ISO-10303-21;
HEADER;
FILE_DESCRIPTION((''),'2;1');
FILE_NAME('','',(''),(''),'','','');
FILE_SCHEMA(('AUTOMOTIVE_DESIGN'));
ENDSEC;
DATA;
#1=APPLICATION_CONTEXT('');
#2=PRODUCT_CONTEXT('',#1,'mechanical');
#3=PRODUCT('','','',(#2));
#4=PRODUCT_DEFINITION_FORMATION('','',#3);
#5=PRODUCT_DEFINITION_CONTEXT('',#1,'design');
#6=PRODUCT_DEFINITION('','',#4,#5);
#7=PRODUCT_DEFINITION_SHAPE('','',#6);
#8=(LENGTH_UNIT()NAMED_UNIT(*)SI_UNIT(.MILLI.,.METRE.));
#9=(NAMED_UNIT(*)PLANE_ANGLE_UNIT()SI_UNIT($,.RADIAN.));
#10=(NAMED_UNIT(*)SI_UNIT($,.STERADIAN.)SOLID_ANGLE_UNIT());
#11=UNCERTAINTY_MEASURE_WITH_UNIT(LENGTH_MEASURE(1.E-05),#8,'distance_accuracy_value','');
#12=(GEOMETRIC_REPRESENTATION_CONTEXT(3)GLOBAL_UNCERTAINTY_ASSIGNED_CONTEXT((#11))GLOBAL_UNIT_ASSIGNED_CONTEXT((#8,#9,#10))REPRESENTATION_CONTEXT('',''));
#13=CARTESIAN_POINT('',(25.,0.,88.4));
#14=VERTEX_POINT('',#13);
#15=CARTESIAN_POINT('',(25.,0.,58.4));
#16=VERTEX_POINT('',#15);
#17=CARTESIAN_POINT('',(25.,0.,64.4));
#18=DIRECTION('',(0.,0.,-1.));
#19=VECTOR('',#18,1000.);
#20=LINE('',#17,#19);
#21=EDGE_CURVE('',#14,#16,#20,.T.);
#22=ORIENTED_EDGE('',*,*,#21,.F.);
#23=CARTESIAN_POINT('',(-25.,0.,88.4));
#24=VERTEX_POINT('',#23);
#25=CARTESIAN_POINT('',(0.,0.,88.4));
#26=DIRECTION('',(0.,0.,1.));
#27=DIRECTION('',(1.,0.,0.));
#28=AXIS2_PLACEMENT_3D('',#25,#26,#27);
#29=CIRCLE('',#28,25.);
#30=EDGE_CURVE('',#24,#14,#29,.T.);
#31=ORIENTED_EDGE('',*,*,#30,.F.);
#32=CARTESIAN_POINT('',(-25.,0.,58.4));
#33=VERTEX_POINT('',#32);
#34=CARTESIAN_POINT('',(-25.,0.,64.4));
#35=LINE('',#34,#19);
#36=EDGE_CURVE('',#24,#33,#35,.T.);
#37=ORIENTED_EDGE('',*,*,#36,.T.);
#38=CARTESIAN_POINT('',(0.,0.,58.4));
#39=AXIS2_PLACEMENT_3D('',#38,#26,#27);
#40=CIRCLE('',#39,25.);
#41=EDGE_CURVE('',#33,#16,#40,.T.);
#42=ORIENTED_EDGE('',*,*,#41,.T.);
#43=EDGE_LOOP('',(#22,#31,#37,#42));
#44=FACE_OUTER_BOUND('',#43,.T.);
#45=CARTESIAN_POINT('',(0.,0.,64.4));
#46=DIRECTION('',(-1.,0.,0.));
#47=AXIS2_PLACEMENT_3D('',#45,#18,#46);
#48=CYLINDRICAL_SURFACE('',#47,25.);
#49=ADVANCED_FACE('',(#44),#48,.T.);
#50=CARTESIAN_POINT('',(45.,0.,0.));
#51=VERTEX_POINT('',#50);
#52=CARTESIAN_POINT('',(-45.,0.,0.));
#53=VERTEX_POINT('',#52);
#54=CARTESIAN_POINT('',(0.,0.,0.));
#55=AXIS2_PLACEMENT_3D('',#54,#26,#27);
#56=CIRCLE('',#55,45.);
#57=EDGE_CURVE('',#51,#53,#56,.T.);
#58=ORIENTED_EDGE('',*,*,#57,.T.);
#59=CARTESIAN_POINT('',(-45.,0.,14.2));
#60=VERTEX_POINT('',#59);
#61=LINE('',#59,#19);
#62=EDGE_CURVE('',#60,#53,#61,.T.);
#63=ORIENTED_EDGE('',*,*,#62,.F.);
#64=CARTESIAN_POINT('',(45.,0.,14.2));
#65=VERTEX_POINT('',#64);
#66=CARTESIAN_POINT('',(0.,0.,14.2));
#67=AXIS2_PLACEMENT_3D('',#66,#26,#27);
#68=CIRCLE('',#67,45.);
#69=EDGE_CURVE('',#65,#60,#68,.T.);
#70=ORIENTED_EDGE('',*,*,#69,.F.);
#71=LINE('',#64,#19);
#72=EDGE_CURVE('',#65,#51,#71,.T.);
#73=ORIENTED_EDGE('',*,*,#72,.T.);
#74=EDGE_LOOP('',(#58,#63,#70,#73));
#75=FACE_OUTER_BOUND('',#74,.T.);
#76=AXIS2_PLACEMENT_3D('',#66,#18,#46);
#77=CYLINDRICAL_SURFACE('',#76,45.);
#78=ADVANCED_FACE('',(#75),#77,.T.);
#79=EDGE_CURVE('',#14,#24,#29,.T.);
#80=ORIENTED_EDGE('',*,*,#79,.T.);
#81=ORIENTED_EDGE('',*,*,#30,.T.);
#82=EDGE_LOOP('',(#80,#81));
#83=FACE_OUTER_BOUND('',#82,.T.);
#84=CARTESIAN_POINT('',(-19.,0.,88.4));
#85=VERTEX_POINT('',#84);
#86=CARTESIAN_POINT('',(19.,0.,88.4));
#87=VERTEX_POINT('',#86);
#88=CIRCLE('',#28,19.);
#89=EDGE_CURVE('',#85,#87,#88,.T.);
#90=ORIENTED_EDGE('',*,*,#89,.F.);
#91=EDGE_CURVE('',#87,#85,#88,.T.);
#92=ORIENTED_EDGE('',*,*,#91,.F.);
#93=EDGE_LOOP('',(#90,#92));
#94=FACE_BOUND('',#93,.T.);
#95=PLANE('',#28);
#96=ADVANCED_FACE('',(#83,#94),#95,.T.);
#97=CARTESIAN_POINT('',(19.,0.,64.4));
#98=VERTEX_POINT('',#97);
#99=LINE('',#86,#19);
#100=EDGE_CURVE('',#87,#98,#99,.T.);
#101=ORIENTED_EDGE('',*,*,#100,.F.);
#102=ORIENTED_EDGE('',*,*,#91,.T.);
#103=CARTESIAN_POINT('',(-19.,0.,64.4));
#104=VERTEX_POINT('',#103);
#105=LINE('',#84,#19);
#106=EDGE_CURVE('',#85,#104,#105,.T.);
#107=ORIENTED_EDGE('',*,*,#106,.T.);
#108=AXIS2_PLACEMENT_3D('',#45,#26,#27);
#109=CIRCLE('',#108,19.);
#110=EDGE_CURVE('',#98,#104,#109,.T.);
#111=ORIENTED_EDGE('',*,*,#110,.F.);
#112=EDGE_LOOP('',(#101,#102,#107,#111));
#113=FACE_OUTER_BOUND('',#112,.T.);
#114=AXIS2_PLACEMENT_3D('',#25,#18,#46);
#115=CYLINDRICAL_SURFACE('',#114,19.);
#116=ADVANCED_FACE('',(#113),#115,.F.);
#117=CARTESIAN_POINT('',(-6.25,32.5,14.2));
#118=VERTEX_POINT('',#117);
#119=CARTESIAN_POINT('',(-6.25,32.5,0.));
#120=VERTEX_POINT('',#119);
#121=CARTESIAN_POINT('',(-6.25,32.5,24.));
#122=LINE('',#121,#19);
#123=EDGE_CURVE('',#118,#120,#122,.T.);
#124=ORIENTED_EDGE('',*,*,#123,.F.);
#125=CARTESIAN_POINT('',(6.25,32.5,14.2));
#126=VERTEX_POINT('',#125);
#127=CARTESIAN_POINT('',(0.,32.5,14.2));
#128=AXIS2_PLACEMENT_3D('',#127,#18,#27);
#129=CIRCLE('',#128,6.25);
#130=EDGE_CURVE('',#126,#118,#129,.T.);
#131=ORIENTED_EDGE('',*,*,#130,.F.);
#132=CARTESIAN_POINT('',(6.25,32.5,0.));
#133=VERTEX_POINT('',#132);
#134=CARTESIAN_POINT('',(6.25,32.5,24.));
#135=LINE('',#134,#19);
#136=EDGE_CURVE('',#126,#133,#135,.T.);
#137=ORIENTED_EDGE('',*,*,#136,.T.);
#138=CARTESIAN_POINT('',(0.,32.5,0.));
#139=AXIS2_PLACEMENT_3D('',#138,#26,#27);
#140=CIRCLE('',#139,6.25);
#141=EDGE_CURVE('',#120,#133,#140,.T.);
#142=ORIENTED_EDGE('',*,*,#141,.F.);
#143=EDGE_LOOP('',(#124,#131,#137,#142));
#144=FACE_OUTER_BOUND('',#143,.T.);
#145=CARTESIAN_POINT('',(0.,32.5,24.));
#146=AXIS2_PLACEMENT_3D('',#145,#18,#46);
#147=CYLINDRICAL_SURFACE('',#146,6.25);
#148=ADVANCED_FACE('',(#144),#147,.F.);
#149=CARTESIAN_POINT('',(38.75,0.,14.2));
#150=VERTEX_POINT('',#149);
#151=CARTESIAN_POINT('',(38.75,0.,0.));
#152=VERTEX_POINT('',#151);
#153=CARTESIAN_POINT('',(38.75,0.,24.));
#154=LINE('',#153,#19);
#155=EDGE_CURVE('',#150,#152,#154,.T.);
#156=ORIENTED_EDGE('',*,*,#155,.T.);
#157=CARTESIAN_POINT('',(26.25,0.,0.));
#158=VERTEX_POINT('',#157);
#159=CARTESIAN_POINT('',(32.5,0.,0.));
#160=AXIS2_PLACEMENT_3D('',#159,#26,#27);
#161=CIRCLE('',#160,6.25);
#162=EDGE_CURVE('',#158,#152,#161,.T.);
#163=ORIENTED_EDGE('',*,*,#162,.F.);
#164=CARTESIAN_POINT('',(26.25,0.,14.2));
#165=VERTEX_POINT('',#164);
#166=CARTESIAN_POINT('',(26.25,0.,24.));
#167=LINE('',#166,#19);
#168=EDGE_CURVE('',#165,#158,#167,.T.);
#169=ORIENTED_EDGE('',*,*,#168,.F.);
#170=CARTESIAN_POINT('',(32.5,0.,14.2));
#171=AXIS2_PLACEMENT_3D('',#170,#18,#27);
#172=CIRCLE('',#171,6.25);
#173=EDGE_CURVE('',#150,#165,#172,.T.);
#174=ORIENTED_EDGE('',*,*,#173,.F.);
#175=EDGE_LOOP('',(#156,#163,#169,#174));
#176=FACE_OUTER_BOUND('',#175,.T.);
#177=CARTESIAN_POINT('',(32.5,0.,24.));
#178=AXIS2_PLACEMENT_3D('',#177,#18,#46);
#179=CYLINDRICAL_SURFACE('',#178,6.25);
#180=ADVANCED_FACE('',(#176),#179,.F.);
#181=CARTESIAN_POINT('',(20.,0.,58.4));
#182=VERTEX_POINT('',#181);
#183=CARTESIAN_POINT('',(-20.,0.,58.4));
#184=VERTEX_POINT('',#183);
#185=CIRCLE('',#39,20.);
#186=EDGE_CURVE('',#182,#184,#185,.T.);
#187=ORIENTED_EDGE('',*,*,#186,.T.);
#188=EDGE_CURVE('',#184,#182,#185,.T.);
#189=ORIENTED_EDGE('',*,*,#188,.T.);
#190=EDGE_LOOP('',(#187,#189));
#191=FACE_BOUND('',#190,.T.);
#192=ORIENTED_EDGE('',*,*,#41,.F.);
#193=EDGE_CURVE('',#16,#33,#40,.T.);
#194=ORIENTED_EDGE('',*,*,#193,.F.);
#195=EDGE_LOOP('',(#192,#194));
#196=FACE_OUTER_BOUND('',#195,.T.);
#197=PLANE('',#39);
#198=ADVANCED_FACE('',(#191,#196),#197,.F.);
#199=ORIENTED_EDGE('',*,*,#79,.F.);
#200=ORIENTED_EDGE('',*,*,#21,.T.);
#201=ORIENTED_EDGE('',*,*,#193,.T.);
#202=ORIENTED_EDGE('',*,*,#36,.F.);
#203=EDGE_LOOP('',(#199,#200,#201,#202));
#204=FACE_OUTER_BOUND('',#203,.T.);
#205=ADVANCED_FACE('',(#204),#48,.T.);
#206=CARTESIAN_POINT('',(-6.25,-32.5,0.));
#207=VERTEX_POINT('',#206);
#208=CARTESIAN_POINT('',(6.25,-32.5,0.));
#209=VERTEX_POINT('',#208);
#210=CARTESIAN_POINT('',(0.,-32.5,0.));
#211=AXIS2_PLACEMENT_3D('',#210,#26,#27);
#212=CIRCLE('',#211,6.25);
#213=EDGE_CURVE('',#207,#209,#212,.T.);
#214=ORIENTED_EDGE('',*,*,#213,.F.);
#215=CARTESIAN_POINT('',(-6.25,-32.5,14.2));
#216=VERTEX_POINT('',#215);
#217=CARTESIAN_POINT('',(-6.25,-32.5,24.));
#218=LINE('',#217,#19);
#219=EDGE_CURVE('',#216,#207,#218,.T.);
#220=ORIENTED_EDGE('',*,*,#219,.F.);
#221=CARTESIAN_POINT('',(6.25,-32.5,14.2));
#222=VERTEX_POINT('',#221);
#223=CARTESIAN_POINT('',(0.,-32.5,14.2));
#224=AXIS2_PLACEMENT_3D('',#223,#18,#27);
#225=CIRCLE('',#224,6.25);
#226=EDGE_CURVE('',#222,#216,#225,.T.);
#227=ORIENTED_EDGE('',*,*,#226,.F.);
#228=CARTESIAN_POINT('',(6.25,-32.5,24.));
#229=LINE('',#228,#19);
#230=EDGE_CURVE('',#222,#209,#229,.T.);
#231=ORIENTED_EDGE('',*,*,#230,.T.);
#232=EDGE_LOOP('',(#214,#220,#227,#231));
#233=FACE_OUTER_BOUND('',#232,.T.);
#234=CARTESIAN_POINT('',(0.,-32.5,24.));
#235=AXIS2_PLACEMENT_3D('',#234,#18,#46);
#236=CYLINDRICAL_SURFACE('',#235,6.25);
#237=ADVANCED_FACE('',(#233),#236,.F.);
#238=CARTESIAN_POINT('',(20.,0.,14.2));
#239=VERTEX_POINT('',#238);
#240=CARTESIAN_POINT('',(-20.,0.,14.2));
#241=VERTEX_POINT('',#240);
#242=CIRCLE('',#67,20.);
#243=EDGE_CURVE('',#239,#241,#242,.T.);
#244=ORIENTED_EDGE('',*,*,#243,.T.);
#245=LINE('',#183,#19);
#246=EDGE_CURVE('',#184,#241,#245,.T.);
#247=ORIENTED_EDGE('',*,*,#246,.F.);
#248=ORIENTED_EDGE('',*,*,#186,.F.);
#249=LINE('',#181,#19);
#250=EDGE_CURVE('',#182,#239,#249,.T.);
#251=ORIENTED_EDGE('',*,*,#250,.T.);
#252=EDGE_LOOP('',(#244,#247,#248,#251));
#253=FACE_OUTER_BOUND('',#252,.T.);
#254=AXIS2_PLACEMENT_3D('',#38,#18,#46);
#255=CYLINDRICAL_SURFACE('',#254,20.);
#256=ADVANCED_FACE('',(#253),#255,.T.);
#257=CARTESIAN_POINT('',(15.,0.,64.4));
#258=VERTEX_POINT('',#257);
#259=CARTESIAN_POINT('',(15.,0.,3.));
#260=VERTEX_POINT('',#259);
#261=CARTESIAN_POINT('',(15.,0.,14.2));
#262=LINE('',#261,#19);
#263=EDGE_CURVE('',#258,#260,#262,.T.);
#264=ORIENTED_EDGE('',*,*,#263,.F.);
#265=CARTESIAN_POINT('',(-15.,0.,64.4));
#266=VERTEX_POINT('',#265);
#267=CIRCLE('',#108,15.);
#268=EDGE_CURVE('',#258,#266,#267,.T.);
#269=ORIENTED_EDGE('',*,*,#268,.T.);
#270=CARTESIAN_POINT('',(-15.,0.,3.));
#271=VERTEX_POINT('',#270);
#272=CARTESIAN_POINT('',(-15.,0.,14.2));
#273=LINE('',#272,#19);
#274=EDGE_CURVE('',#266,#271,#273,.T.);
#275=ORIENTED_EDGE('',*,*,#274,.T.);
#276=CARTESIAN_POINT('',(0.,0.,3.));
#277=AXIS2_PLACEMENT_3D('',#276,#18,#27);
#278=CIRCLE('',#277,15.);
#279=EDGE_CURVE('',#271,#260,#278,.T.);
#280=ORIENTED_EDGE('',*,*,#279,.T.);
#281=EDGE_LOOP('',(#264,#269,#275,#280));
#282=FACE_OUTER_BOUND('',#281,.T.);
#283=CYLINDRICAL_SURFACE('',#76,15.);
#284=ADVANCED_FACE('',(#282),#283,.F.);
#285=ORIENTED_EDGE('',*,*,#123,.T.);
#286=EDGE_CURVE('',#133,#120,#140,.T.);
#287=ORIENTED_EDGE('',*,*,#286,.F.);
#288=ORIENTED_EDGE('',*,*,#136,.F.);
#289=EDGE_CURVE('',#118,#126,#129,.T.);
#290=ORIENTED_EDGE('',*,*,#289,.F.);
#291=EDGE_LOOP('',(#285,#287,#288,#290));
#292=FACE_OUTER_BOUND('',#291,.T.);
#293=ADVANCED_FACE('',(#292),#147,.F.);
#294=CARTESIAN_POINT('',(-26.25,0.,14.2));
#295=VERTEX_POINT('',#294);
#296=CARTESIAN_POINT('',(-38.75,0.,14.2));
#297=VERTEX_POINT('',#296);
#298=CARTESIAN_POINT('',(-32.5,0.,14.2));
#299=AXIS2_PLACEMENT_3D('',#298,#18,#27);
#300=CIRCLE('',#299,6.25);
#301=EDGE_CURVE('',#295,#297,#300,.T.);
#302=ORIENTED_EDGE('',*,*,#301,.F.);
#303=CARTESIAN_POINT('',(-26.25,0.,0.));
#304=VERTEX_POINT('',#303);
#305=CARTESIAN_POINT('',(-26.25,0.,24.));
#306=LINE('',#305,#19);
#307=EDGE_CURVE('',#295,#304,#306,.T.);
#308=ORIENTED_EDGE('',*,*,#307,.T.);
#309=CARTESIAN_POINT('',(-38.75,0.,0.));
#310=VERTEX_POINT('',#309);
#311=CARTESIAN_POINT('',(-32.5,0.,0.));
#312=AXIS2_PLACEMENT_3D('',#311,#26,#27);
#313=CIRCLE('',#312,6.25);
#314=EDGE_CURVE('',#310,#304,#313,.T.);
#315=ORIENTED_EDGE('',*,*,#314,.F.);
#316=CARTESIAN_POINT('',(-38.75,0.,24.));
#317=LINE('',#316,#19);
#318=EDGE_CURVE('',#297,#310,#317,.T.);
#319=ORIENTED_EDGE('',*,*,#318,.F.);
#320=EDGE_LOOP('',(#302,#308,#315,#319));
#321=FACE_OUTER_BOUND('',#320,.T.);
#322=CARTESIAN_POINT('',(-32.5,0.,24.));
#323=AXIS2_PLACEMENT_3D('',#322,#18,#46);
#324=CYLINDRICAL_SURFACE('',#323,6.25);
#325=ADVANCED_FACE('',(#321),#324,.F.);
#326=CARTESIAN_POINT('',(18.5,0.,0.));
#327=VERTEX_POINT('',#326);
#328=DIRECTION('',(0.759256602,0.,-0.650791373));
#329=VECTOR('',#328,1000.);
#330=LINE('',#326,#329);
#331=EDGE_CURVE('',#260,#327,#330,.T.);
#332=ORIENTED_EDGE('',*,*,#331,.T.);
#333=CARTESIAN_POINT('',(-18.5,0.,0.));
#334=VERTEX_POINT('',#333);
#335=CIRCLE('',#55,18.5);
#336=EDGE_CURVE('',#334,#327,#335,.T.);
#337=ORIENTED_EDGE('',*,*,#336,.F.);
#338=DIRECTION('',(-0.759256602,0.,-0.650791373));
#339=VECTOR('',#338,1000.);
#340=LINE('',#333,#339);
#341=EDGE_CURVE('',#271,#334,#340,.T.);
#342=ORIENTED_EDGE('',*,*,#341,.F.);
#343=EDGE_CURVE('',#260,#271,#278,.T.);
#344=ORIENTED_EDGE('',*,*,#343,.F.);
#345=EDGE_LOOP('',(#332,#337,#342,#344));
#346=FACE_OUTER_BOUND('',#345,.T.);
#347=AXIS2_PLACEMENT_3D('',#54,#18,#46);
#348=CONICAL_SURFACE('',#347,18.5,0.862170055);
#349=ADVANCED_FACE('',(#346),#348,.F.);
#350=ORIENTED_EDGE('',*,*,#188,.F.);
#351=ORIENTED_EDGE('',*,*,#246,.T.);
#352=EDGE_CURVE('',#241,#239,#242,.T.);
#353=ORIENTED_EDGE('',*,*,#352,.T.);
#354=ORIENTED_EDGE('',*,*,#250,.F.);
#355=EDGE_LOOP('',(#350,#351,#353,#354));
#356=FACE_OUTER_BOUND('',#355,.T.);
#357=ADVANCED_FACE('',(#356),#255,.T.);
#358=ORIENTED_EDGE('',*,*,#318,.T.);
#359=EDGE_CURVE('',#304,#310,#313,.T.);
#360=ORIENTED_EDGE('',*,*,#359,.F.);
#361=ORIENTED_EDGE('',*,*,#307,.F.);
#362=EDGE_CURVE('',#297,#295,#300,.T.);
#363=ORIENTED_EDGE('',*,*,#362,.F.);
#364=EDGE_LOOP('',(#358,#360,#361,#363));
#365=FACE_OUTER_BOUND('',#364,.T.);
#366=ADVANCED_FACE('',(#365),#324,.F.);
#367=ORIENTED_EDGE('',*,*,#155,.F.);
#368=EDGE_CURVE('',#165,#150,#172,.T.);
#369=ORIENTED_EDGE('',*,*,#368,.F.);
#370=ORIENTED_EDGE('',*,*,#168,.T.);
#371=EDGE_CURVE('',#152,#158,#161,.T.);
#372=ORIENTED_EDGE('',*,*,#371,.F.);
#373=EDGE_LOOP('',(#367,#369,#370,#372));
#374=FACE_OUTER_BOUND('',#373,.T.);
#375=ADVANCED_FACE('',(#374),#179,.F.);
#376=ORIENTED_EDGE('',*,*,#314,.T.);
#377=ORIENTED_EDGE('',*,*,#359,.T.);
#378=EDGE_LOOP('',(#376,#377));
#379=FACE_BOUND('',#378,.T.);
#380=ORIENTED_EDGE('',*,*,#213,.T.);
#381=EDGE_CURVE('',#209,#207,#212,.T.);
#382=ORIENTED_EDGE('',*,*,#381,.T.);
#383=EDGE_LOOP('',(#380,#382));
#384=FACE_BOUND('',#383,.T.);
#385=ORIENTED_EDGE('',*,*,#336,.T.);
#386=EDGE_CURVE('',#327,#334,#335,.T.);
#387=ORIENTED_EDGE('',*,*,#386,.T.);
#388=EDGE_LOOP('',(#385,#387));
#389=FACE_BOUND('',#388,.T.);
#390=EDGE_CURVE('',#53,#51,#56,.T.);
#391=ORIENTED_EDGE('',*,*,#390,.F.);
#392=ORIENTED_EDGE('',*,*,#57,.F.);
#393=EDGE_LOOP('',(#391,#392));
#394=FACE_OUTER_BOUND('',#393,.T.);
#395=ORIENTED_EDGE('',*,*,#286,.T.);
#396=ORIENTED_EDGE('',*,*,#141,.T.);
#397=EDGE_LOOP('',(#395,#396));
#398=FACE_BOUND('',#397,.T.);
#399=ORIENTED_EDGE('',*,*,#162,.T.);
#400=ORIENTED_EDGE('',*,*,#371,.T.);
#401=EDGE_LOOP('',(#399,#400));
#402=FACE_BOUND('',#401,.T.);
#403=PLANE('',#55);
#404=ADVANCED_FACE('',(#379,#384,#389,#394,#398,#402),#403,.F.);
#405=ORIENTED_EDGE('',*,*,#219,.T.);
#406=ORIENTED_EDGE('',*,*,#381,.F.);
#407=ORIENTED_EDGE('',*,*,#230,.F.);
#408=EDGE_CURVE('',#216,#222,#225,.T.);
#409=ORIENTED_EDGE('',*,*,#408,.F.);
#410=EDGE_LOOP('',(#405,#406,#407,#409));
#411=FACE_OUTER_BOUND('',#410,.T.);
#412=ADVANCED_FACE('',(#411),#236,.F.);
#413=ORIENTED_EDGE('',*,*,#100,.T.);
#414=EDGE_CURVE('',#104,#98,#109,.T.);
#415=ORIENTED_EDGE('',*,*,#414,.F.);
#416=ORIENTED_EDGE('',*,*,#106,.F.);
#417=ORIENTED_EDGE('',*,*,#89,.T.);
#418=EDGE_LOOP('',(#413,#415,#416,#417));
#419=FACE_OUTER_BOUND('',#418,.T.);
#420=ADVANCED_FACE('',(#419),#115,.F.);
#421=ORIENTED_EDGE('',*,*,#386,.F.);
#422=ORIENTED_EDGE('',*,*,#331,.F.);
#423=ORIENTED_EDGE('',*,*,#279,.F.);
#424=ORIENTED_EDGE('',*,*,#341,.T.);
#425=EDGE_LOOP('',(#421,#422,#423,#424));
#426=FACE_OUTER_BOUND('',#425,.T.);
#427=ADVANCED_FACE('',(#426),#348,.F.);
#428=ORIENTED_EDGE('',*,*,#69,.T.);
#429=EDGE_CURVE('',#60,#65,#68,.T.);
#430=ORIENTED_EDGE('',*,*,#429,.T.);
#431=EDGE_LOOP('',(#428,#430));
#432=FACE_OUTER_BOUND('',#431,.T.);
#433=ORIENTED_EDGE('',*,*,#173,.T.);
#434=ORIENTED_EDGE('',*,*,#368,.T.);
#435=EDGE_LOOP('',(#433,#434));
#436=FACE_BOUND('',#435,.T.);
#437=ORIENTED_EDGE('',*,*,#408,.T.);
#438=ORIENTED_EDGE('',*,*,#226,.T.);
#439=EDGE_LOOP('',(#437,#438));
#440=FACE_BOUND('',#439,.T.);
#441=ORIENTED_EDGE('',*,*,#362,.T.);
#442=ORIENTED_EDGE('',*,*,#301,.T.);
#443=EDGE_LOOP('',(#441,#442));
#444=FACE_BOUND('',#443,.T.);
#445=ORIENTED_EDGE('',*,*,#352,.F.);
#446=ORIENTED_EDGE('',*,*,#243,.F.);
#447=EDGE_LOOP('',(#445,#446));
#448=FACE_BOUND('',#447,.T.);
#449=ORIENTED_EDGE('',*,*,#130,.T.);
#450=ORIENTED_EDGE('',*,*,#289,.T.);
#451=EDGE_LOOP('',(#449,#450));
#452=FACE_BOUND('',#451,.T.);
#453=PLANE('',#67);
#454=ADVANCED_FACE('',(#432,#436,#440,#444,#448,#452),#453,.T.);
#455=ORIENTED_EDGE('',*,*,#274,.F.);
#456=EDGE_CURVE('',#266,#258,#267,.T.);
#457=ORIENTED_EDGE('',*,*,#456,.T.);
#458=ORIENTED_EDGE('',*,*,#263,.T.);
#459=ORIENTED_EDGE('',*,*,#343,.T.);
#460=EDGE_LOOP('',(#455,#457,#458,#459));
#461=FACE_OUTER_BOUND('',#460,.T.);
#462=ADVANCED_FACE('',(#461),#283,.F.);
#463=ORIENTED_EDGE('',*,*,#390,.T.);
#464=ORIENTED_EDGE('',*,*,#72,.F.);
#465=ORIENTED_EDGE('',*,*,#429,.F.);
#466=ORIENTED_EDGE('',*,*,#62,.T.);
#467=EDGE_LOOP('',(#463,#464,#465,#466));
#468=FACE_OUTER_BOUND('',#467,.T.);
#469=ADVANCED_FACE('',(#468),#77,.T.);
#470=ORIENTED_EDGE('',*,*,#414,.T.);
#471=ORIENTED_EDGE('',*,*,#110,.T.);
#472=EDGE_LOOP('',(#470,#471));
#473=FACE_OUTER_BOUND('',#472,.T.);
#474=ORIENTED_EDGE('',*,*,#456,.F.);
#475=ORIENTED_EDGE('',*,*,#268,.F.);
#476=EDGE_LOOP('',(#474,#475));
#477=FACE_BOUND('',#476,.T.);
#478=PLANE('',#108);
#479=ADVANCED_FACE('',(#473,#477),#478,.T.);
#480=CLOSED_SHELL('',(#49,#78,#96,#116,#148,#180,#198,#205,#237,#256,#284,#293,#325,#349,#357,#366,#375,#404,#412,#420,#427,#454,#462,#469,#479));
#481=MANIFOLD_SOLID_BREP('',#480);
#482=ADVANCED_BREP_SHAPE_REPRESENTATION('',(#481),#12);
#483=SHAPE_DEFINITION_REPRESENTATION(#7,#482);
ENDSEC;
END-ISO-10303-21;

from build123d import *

# Parameters (mm, degrees)
FLANGE_SKETCH_R             = 45
FLANGE_SKETCH_R_2           = 15
FLANGE_90_DEPTH             = 14.2
HUB_SKETCH_R                = 20
HUB_SKETCH_R_2              = 15
HUB_40_DEPTH                = 44.2
COLLAR_SKETCH_R             = 25
COLLAR_SKETCH_R_2           = 15
COLLAR_50_DEPTH             = 6
END_SLEEVE_SKETCH_R         = 25
END_SLEEVE_SKETCH_R_2       = 19
END_SLEEVE_50_BORE_38_DEPTH = 24
FLANGE_EDGE_CHAMFER_SIZE    = 3
FLANGE_EDGE_CHAMFER_SIZE2   = 3.5
BOLT_HOLES_SET_A_SKETCH_R   = 6.25
BOLT_HOLES_SET_A_DEPTH      = 24
BOLT_HOLES_SET_B_SKETCH_R   = 6.25
BOLT_HOLES_SET_B_DEPTH      = 24


with BuildPart() as part:
    # Flange Sketch → Flange Ø90 (new body)
    with BuildSketch(Plane.XY):
        Circle(FLANGE_SKETCH_R)
        Circle(FLANGE_SKETCH_R_2, mode=Mode.SUBTRACT)
    extrude(amount=FLANGE_90_DEPTH)

    # Hub Sketch → Hub Ø40 (add)
    with BuildSketch(Plane.XY.offset(14.2)):
        Circle(HUB_SKETCH_R)
        Circle(HUB_SKETCH_R_2, mode=Mode.SUBTRACT)
    extrude(amount=HUB_40_DEPTH)

    # Collar Sketch → Collar Ø50 (add)
    with BuildSketch(Plane.XY.offset(58.4)):
        Circle(COLLAR_SKETCH_R)
        Circle(COLLAR_SKETCH_R_2, mode=Mode.SUBTRACT)
    extrude(amount=COLLAR_50_DEPTH)

    # End Sleeve Sketch → End Sleeve Ø50 Bore Ø38 (add)
    with BuildSketch(Plane.XY.offset(64.4)):
        Circle(END_SLEEVE_SKETCH_R)
        Circle(END_SLEEVE_SKETCH_R_2, mode=Mode.SUBTRACT)
    extrude(amount=END_SLEEVE_50_BORE_38_DEPTH)

    # Flange Edge Chamfer
    flange_edge_chamfer_edges = [part.edges().sort_by_distance(p)[0] for p in [
        (-15, 0, 0),
    ]]
    flange_edge_chamfer_side = [part.faces().sort_by_distance(p)[0] for p in [
        (-15, 0, 32.2),
    ]]
    chamfer(flange_edge_chamfer_edges, length=FLANGE_EDGE_CHAMFER_SIZE, length2=FLANGE_EDGE_CHAMFER_SIZE2, reference=flange_edge_chamfer_side[0])

    # Bolt Holes Set A Sketch → Bolt Holes Set A (cut)
    with BuildSketch(Plane.XY):
        with Locations((0, 32.5)):
            Circle(BOLT_HOLES_SET_A_SKETCH_R)
        with Locations((0, -32.5)):
            Circle(BOLT_HOLES_SET_A_SKETCH_R)
    extrude(amount=BOLT_HOLES_SET_A_DEPTH, mode=Mode.SUBTRACT)

    # Bolt Holes Set B Sketch → Bolt Holes Set B (cut)
    with BuildSketch(Plane.XY):
        with Locations((-32.5, 0)):
            Circle(BOLT_HOLES_SET_B_SKETCH_R)
        with Locations((32.5, 0)):
            Circle(BOLT_HOLES_SET_B_SKETCH_R)
    extrude(amount=BOLT_HOLES_SET_B_DEPTH, mode=Mode.SUBTRACT)


solid = part.part
